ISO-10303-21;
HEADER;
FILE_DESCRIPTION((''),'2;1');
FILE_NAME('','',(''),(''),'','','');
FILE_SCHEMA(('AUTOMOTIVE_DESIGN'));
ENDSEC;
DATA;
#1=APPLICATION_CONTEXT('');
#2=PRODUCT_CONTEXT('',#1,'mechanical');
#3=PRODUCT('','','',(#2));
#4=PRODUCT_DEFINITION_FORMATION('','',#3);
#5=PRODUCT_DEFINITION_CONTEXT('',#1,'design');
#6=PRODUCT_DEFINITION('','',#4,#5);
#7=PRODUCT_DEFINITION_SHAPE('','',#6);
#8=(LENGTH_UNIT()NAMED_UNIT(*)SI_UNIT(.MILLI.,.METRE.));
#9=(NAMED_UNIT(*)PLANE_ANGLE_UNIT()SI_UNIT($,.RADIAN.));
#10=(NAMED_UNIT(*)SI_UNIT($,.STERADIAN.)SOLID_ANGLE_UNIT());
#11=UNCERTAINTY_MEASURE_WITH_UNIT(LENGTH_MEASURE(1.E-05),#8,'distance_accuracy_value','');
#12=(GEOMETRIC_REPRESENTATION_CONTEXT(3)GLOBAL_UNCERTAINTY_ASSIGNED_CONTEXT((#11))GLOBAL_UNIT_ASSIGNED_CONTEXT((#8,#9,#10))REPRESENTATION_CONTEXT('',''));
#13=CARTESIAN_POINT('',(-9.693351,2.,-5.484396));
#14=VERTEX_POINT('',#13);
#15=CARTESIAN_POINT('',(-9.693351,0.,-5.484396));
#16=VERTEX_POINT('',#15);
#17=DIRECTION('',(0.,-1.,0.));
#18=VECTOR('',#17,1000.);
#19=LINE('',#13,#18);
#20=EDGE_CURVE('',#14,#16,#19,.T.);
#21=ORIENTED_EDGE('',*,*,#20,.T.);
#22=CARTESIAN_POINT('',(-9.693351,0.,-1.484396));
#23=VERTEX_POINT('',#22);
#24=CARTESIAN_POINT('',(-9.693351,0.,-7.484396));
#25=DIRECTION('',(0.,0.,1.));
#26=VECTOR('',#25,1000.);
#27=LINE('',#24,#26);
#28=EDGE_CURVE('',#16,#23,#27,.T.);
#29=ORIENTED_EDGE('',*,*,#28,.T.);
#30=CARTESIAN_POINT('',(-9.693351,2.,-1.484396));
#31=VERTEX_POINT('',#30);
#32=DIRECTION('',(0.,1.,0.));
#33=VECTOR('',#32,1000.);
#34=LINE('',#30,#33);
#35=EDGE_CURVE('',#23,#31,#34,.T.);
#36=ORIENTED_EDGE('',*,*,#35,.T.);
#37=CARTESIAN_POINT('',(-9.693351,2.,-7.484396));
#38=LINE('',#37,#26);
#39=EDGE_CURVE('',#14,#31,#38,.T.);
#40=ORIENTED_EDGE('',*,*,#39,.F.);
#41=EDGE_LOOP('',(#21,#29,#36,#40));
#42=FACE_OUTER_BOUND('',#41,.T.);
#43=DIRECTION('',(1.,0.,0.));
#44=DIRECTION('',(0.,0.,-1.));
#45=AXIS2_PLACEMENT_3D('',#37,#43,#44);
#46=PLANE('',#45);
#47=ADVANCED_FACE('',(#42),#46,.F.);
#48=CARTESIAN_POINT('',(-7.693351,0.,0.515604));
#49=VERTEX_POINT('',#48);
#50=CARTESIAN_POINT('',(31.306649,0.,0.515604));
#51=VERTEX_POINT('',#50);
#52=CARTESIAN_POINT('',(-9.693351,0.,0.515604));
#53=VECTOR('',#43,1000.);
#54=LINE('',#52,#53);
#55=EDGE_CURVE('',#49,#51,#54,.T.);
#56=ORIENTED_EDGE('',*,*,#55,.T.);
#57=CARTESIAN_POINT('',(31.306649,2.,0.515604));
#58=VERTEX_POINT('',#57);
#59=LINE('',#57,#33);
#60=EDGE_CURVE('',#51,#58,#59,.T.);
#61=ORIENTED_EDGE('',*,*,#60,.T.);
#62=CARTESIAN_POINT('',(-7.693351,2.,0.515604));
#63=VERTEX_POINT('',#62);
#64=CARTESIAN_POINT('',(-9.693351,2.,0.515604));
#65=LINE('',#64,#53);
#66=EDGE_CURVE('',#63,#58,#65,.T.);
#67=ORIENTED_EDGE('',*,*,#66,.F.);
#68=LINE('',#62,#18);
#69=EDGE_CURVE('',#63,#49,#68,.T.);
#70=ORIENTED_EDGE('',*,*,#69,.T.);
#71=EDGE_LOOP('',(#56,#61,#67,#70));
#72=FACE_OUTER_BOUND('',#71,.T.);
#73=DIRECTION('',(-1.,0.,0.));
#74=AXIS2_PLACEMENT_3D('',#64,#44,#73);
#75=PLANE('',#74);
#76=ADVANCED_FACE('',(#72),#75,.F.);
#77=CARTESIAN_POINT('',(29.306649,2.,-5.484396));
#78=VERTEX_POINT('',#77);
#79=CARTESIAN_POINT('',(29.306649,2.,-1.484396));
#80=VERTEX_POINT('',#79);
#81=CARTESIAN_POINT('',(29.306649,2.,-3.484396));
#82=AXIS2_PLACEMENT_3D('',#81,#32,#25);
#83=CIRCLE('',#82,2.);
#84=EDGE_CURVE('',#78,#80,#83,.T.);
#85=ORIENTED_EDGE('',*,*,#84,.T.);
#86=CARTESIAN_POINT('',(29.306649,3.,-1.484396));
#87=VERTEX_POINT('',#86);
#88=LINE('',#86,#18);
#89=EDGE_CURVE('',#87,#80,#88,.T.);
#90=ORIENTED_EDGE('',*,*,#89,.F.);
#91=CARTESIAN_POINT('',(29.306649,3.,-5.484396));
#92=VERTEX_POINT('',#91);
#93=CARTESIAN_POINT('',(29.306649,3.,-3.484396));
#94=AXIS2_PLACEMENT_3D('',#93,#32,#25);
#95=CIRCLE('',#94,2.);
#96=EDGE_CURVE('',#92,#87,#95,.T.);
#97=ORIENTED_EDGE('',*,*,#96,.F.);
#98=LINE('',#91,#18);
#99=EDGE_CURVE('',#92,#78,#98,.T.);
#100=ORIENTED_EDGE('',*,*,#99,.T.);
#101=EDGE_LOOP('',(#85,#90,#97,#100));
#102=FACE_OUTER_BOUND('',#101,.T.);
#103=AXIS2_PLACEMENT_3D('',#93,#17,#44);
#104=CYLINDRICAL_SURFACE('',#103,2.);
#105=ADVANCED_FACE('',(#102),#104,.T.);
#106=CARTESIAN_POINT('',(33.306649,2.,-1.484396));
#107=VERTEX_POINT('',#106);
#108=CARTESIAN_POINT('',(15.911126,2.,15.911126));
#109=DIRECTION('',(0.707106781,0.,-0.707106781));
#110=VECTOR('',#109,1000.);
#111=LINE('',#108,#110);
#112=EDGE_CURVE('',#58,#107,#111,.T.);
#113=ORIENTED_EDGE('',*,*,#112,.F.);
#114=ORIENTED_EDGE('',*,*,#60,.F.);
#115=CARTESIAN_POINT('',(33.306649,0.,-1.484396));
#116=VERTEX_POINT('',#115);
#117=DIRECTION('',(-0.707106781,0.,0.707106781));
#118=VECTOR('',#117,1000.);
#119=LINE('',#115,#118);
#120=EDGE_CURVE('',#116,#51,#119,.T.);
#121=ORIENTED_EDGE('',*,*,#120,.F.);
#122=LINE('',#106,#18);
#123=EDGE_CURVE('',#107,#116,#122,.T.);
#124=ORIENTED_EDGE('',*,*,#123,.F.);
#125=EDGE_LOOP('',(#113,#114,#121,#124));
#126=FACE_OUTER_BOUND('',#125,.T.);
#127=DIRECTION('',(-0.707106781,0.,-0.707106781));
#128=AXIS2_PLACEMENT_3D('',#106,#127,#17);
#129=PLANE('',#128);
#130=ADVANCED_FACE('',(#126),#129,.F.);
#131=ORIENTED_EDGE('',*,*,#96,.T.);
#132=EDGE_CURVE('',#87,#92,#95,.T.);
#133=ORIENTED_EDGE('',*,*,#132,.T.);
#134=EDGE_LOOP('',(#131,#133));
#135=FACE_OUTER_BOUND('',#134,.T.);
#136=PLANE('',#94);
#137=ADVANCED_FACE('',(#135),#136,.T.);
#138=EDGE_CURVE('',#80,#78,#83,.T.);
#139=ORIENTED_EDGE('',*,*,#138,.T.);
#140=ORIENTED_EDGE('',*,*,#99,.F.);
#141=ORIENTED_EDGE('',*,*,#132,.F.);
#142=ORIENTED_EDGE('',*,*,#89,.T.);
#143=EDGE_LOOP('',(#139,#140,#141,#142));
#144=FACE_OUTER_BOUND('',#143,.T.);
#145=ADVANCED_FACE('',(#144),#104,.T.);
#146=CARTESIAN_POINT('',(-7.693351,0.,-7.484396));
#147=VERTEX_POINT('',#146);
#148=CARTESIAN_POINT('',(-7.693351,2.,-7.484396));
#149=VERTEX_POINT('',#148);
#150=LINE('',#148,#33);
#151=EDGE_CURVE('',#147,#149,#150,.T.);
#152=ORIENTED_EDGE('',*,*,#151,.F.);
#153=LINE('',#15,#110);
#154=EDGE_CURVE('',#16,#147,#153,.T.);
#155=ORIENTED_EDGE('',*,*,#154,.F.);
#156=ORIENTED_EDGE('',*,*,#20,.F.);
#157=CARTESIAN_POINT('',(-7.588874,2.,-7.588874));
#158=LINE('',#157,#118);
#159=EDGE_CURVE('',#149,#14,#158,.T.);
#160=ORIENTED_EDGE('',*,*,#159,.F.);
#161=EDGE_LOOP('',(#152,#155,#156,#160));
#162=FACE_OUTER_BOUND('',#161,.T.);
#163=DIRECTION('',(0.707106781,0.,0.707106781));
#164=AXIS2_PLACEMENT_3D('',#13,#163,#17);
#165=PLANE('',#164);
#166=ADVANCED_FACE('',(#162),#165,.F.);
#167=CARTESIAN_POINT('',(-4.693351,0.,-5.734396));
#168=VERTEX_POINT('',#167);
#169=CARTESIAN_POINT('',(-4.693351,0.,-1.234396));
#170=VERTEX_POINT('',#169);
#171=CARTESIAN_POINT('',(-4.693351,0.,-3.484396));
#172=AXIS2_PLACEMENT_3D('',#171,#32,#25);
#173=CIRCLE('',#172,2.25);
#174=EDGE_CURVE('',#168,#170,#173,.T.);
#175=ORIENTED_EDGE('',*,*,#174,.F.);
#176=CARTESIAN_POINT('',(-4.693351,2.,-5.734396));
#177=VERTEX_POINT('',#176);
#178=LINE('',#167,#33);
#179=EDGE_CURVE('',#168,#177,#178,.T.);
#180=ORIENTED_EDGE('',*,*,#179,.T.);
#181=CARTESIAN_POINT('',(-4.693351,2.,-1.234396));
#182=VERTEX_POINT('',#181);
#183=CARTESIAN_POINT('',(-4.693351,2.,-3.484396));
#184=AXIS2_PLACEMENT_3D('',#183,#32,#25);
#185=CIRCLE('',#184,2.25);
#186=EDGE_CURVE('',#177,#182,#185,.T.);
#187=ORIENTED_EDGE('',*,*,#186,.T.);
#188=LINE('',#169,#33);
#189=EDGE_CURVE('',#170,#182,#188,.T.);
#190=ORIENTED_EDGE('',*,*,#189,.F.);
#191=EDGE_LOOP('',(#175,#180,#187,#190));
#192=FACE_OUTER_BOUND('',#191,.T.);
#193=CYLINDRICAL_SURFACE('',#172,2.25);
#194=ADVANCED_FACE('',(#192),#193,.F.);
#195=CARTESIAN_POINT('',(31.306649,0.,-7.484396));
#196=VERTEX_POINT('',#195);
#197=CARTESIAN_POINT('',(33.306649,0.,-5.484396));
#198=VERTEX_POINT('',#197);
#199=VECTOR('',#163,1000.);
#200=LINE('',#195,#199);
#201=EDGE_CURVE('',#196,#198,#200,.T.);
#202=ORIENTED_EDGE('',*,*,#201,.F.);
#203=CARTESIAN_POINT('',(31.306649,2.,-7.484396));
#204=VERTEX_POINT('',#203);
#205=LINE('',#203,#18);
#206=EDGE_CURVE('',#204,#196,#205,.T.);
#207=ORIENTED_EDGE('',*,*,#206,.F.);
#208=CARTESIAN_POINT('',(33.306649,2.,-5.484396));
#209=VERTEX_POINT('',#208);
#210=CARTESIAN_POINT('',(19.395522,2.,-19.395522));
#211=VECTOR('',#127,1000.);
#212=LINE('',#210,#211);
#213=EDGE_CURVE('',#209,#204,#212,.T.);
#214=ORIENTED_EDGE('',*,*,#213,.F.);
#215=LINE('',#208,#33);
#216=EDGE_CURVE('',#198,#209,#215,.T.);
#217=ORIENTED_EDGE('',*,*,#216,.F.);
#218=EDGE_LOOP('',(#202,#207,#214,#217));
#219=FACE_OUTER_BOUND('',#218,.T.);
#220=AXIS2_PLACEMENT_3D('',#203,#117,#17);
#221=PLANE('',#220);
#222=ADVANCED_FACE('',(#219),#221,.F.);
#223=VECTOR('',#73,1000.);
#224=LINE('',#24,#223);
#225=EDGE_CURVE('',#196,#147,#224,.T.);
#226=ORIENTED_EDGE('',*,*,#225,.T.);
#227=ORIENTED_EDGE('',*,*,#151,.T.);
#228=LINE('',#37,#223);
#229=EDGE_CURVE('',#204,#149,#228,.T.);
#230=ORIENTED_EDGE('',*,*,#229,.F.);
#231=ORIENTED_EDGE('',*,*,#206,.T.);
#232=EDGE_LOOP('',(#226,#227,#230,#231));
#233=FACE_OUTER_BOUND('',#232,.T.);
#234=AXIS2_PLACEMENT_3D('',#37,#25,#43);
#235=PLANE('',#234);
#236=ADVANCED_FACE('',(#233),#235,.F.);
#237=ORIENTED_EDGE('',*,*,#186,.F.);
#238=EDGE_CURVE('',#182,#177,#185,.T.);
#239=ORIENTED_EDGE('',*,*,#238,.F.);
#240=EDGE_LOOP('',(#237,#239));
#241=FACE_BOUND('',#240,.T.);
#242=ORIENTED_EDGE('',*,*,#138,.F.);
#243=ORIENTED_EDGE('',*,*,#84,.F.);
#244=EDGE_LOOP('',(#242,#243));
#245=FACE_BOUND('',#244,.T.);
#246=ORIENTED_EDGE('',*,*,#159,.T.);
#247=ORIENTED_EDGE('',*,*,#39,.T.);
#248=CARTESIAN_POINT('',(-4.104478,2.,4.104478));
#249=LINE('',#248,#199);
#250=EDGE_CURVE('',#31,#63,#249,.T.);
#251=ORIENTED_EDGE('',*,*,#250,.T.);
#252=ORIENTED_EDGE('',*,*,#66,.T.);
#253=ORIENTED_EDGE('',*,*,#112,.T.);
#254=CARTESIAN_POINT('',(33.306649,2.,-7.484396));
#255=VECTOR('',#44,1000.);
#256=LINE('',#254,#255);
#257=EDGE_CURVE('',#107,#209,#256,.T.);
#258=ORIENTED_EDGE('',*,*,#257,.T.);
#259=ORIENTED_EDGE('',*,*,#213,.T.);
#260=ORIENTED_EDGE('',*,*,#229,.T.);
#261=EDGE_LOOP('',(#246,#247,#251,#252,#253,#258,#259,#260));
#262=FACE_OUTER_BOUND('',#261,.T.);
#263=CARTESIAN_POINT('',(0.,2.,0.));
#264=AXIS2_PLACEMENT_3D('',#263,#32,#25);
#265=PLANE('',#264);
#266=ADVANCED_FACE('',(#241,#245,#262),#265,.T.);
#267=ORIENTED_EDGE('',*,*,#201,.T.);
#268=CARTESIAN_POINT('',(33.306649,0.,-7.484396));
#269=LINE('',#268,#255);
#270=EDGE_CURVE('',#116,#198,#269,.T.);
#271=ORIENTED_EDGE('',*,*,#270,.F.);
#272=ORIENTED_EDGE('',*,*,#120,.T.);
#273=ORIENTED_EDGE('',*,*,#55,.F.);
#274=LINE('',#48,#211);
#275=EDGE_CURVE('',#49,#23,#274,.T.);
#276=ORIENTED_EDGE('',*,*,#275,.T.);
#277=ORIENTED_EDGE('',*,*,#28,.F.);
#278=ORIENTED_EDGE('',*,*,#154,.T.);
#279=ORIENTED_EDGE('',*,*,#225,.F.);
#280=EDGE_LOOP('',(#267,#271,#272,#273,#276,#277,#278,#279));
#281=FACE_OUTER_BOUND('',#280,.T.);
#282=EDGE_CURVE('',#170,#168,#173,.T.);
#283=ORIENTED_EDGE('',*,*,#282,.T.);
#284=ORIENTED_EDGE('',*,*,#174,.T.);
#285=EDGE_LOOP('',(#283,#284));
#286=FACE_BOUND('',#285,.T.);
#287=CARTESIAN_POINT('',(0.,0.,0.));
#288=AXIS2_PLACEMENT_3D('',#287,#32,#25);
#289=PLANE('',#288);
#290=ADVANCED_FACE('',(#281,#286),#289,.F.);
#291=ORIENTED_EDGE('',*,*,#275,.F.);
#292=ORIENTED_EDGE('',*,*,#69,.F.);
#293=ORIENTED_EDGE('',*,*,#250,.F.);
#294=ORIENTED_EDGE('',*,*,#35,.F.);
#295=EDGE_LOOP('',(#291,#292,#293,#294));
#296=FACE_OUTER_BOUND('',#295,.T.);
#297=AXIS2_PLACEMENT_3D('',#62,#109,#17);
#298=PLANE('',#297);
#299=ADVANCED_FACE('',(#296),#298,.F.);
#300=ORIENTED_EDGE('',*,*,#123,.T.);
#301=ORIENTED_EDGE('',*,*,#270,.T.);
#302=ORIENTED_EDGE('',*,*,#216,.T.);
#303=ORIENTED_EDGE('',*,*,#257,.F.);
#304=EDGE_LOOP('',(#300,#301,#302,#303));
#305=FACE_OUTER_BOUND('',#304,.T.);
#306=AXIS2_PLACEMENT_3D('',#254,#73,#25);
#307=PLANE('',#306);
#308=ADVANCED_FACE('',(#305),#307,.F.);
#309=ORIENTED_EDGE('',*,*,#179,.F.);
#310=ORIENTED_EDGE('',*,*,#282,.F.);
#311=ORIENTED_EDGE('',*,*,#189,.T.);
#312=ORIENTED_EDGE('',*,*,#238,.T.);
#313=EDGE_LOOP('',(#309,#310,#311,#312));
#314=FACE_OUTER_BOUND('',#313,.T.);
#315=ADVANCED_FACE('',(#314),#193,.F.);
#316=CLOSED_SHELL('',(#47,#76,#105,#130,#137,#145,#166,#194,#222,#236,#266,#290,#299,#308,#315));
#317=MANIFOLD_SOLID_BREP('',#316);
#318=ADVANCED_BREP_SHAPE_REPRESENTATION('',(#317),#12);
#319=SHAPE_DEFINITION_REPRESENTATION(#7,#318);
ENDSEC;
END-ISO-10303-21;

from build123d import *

# Parameters (mm, degrees)
SKETCH1_W           = 43
SKETCH1_H           = 8
BOSS_EXTRUDE1_DEPTH = 2
SKETCH2_R           = 2.25
CUT_EXTRUDE1_DEPTH  = 35.195745727
SKETCH3_R           = 2
BOSS_EXTRUDE2_DEPTH = 1
CHAMFER2_SIZE       = 2


with BuildPart() as part:
    # Sketch1 → Boss-Extrude1 (new body)
    with BuildSketch(Plane(origin=(0, 0, 0), x_dir=(1, 0, 0), z_dir=(0, 1, 0))):
        with Locations((11.806648575, 3.484396201)):
            Rectangle(SKETCH1_W, SKETCH1_H)
    extrude(amount=BOSS_EXTRUDE1_DEPTH)

    # Sketch2 → Cut-Extrude1 (cut, through all)
    with BuildSketch(Plane(origin=(0, 2, 0), x_dir=(1, 0, 0), z_dir=(0, 1, 0))):
        with Locations(Location((-4.693351425, 3.484396201, 0), (0, 0, 270))):
            Circle(SKETCH2_R)
    extrude(amount=-CUT_EXTRUDE1_DEPTH, mode=Mode.SUBTRACT)

    # Sketch3 → Boss-Extrude2 (add)
    with BuildSketch(Plane(origin=(0, 2, 0), x_dir=(1, 0, 0), z_dir=(0, 1, 0))):
        with Locations(Location((29.306648575, 3.484396201, 0), (0, 0, 270))):
            Circle(SKETCH3_R)
    extrude(amount=BOSS_EXTRUDE2_DEPTH)

    # Chamfer2
    chamfer2_edges = [part.edges().sort_by_distance(p)[0] for p in [
        (-9.693351425, 1, -7.484396201),
        (33.306648575, 1, -7.484396201),
        (33.306648575, 1, 0.515603799),
        (-9.693351425, 1, 0.515603799),
    ]]
    chamfer(chamfer2_edges, length=CHAMFER2_SIZE)


solid = part.part
